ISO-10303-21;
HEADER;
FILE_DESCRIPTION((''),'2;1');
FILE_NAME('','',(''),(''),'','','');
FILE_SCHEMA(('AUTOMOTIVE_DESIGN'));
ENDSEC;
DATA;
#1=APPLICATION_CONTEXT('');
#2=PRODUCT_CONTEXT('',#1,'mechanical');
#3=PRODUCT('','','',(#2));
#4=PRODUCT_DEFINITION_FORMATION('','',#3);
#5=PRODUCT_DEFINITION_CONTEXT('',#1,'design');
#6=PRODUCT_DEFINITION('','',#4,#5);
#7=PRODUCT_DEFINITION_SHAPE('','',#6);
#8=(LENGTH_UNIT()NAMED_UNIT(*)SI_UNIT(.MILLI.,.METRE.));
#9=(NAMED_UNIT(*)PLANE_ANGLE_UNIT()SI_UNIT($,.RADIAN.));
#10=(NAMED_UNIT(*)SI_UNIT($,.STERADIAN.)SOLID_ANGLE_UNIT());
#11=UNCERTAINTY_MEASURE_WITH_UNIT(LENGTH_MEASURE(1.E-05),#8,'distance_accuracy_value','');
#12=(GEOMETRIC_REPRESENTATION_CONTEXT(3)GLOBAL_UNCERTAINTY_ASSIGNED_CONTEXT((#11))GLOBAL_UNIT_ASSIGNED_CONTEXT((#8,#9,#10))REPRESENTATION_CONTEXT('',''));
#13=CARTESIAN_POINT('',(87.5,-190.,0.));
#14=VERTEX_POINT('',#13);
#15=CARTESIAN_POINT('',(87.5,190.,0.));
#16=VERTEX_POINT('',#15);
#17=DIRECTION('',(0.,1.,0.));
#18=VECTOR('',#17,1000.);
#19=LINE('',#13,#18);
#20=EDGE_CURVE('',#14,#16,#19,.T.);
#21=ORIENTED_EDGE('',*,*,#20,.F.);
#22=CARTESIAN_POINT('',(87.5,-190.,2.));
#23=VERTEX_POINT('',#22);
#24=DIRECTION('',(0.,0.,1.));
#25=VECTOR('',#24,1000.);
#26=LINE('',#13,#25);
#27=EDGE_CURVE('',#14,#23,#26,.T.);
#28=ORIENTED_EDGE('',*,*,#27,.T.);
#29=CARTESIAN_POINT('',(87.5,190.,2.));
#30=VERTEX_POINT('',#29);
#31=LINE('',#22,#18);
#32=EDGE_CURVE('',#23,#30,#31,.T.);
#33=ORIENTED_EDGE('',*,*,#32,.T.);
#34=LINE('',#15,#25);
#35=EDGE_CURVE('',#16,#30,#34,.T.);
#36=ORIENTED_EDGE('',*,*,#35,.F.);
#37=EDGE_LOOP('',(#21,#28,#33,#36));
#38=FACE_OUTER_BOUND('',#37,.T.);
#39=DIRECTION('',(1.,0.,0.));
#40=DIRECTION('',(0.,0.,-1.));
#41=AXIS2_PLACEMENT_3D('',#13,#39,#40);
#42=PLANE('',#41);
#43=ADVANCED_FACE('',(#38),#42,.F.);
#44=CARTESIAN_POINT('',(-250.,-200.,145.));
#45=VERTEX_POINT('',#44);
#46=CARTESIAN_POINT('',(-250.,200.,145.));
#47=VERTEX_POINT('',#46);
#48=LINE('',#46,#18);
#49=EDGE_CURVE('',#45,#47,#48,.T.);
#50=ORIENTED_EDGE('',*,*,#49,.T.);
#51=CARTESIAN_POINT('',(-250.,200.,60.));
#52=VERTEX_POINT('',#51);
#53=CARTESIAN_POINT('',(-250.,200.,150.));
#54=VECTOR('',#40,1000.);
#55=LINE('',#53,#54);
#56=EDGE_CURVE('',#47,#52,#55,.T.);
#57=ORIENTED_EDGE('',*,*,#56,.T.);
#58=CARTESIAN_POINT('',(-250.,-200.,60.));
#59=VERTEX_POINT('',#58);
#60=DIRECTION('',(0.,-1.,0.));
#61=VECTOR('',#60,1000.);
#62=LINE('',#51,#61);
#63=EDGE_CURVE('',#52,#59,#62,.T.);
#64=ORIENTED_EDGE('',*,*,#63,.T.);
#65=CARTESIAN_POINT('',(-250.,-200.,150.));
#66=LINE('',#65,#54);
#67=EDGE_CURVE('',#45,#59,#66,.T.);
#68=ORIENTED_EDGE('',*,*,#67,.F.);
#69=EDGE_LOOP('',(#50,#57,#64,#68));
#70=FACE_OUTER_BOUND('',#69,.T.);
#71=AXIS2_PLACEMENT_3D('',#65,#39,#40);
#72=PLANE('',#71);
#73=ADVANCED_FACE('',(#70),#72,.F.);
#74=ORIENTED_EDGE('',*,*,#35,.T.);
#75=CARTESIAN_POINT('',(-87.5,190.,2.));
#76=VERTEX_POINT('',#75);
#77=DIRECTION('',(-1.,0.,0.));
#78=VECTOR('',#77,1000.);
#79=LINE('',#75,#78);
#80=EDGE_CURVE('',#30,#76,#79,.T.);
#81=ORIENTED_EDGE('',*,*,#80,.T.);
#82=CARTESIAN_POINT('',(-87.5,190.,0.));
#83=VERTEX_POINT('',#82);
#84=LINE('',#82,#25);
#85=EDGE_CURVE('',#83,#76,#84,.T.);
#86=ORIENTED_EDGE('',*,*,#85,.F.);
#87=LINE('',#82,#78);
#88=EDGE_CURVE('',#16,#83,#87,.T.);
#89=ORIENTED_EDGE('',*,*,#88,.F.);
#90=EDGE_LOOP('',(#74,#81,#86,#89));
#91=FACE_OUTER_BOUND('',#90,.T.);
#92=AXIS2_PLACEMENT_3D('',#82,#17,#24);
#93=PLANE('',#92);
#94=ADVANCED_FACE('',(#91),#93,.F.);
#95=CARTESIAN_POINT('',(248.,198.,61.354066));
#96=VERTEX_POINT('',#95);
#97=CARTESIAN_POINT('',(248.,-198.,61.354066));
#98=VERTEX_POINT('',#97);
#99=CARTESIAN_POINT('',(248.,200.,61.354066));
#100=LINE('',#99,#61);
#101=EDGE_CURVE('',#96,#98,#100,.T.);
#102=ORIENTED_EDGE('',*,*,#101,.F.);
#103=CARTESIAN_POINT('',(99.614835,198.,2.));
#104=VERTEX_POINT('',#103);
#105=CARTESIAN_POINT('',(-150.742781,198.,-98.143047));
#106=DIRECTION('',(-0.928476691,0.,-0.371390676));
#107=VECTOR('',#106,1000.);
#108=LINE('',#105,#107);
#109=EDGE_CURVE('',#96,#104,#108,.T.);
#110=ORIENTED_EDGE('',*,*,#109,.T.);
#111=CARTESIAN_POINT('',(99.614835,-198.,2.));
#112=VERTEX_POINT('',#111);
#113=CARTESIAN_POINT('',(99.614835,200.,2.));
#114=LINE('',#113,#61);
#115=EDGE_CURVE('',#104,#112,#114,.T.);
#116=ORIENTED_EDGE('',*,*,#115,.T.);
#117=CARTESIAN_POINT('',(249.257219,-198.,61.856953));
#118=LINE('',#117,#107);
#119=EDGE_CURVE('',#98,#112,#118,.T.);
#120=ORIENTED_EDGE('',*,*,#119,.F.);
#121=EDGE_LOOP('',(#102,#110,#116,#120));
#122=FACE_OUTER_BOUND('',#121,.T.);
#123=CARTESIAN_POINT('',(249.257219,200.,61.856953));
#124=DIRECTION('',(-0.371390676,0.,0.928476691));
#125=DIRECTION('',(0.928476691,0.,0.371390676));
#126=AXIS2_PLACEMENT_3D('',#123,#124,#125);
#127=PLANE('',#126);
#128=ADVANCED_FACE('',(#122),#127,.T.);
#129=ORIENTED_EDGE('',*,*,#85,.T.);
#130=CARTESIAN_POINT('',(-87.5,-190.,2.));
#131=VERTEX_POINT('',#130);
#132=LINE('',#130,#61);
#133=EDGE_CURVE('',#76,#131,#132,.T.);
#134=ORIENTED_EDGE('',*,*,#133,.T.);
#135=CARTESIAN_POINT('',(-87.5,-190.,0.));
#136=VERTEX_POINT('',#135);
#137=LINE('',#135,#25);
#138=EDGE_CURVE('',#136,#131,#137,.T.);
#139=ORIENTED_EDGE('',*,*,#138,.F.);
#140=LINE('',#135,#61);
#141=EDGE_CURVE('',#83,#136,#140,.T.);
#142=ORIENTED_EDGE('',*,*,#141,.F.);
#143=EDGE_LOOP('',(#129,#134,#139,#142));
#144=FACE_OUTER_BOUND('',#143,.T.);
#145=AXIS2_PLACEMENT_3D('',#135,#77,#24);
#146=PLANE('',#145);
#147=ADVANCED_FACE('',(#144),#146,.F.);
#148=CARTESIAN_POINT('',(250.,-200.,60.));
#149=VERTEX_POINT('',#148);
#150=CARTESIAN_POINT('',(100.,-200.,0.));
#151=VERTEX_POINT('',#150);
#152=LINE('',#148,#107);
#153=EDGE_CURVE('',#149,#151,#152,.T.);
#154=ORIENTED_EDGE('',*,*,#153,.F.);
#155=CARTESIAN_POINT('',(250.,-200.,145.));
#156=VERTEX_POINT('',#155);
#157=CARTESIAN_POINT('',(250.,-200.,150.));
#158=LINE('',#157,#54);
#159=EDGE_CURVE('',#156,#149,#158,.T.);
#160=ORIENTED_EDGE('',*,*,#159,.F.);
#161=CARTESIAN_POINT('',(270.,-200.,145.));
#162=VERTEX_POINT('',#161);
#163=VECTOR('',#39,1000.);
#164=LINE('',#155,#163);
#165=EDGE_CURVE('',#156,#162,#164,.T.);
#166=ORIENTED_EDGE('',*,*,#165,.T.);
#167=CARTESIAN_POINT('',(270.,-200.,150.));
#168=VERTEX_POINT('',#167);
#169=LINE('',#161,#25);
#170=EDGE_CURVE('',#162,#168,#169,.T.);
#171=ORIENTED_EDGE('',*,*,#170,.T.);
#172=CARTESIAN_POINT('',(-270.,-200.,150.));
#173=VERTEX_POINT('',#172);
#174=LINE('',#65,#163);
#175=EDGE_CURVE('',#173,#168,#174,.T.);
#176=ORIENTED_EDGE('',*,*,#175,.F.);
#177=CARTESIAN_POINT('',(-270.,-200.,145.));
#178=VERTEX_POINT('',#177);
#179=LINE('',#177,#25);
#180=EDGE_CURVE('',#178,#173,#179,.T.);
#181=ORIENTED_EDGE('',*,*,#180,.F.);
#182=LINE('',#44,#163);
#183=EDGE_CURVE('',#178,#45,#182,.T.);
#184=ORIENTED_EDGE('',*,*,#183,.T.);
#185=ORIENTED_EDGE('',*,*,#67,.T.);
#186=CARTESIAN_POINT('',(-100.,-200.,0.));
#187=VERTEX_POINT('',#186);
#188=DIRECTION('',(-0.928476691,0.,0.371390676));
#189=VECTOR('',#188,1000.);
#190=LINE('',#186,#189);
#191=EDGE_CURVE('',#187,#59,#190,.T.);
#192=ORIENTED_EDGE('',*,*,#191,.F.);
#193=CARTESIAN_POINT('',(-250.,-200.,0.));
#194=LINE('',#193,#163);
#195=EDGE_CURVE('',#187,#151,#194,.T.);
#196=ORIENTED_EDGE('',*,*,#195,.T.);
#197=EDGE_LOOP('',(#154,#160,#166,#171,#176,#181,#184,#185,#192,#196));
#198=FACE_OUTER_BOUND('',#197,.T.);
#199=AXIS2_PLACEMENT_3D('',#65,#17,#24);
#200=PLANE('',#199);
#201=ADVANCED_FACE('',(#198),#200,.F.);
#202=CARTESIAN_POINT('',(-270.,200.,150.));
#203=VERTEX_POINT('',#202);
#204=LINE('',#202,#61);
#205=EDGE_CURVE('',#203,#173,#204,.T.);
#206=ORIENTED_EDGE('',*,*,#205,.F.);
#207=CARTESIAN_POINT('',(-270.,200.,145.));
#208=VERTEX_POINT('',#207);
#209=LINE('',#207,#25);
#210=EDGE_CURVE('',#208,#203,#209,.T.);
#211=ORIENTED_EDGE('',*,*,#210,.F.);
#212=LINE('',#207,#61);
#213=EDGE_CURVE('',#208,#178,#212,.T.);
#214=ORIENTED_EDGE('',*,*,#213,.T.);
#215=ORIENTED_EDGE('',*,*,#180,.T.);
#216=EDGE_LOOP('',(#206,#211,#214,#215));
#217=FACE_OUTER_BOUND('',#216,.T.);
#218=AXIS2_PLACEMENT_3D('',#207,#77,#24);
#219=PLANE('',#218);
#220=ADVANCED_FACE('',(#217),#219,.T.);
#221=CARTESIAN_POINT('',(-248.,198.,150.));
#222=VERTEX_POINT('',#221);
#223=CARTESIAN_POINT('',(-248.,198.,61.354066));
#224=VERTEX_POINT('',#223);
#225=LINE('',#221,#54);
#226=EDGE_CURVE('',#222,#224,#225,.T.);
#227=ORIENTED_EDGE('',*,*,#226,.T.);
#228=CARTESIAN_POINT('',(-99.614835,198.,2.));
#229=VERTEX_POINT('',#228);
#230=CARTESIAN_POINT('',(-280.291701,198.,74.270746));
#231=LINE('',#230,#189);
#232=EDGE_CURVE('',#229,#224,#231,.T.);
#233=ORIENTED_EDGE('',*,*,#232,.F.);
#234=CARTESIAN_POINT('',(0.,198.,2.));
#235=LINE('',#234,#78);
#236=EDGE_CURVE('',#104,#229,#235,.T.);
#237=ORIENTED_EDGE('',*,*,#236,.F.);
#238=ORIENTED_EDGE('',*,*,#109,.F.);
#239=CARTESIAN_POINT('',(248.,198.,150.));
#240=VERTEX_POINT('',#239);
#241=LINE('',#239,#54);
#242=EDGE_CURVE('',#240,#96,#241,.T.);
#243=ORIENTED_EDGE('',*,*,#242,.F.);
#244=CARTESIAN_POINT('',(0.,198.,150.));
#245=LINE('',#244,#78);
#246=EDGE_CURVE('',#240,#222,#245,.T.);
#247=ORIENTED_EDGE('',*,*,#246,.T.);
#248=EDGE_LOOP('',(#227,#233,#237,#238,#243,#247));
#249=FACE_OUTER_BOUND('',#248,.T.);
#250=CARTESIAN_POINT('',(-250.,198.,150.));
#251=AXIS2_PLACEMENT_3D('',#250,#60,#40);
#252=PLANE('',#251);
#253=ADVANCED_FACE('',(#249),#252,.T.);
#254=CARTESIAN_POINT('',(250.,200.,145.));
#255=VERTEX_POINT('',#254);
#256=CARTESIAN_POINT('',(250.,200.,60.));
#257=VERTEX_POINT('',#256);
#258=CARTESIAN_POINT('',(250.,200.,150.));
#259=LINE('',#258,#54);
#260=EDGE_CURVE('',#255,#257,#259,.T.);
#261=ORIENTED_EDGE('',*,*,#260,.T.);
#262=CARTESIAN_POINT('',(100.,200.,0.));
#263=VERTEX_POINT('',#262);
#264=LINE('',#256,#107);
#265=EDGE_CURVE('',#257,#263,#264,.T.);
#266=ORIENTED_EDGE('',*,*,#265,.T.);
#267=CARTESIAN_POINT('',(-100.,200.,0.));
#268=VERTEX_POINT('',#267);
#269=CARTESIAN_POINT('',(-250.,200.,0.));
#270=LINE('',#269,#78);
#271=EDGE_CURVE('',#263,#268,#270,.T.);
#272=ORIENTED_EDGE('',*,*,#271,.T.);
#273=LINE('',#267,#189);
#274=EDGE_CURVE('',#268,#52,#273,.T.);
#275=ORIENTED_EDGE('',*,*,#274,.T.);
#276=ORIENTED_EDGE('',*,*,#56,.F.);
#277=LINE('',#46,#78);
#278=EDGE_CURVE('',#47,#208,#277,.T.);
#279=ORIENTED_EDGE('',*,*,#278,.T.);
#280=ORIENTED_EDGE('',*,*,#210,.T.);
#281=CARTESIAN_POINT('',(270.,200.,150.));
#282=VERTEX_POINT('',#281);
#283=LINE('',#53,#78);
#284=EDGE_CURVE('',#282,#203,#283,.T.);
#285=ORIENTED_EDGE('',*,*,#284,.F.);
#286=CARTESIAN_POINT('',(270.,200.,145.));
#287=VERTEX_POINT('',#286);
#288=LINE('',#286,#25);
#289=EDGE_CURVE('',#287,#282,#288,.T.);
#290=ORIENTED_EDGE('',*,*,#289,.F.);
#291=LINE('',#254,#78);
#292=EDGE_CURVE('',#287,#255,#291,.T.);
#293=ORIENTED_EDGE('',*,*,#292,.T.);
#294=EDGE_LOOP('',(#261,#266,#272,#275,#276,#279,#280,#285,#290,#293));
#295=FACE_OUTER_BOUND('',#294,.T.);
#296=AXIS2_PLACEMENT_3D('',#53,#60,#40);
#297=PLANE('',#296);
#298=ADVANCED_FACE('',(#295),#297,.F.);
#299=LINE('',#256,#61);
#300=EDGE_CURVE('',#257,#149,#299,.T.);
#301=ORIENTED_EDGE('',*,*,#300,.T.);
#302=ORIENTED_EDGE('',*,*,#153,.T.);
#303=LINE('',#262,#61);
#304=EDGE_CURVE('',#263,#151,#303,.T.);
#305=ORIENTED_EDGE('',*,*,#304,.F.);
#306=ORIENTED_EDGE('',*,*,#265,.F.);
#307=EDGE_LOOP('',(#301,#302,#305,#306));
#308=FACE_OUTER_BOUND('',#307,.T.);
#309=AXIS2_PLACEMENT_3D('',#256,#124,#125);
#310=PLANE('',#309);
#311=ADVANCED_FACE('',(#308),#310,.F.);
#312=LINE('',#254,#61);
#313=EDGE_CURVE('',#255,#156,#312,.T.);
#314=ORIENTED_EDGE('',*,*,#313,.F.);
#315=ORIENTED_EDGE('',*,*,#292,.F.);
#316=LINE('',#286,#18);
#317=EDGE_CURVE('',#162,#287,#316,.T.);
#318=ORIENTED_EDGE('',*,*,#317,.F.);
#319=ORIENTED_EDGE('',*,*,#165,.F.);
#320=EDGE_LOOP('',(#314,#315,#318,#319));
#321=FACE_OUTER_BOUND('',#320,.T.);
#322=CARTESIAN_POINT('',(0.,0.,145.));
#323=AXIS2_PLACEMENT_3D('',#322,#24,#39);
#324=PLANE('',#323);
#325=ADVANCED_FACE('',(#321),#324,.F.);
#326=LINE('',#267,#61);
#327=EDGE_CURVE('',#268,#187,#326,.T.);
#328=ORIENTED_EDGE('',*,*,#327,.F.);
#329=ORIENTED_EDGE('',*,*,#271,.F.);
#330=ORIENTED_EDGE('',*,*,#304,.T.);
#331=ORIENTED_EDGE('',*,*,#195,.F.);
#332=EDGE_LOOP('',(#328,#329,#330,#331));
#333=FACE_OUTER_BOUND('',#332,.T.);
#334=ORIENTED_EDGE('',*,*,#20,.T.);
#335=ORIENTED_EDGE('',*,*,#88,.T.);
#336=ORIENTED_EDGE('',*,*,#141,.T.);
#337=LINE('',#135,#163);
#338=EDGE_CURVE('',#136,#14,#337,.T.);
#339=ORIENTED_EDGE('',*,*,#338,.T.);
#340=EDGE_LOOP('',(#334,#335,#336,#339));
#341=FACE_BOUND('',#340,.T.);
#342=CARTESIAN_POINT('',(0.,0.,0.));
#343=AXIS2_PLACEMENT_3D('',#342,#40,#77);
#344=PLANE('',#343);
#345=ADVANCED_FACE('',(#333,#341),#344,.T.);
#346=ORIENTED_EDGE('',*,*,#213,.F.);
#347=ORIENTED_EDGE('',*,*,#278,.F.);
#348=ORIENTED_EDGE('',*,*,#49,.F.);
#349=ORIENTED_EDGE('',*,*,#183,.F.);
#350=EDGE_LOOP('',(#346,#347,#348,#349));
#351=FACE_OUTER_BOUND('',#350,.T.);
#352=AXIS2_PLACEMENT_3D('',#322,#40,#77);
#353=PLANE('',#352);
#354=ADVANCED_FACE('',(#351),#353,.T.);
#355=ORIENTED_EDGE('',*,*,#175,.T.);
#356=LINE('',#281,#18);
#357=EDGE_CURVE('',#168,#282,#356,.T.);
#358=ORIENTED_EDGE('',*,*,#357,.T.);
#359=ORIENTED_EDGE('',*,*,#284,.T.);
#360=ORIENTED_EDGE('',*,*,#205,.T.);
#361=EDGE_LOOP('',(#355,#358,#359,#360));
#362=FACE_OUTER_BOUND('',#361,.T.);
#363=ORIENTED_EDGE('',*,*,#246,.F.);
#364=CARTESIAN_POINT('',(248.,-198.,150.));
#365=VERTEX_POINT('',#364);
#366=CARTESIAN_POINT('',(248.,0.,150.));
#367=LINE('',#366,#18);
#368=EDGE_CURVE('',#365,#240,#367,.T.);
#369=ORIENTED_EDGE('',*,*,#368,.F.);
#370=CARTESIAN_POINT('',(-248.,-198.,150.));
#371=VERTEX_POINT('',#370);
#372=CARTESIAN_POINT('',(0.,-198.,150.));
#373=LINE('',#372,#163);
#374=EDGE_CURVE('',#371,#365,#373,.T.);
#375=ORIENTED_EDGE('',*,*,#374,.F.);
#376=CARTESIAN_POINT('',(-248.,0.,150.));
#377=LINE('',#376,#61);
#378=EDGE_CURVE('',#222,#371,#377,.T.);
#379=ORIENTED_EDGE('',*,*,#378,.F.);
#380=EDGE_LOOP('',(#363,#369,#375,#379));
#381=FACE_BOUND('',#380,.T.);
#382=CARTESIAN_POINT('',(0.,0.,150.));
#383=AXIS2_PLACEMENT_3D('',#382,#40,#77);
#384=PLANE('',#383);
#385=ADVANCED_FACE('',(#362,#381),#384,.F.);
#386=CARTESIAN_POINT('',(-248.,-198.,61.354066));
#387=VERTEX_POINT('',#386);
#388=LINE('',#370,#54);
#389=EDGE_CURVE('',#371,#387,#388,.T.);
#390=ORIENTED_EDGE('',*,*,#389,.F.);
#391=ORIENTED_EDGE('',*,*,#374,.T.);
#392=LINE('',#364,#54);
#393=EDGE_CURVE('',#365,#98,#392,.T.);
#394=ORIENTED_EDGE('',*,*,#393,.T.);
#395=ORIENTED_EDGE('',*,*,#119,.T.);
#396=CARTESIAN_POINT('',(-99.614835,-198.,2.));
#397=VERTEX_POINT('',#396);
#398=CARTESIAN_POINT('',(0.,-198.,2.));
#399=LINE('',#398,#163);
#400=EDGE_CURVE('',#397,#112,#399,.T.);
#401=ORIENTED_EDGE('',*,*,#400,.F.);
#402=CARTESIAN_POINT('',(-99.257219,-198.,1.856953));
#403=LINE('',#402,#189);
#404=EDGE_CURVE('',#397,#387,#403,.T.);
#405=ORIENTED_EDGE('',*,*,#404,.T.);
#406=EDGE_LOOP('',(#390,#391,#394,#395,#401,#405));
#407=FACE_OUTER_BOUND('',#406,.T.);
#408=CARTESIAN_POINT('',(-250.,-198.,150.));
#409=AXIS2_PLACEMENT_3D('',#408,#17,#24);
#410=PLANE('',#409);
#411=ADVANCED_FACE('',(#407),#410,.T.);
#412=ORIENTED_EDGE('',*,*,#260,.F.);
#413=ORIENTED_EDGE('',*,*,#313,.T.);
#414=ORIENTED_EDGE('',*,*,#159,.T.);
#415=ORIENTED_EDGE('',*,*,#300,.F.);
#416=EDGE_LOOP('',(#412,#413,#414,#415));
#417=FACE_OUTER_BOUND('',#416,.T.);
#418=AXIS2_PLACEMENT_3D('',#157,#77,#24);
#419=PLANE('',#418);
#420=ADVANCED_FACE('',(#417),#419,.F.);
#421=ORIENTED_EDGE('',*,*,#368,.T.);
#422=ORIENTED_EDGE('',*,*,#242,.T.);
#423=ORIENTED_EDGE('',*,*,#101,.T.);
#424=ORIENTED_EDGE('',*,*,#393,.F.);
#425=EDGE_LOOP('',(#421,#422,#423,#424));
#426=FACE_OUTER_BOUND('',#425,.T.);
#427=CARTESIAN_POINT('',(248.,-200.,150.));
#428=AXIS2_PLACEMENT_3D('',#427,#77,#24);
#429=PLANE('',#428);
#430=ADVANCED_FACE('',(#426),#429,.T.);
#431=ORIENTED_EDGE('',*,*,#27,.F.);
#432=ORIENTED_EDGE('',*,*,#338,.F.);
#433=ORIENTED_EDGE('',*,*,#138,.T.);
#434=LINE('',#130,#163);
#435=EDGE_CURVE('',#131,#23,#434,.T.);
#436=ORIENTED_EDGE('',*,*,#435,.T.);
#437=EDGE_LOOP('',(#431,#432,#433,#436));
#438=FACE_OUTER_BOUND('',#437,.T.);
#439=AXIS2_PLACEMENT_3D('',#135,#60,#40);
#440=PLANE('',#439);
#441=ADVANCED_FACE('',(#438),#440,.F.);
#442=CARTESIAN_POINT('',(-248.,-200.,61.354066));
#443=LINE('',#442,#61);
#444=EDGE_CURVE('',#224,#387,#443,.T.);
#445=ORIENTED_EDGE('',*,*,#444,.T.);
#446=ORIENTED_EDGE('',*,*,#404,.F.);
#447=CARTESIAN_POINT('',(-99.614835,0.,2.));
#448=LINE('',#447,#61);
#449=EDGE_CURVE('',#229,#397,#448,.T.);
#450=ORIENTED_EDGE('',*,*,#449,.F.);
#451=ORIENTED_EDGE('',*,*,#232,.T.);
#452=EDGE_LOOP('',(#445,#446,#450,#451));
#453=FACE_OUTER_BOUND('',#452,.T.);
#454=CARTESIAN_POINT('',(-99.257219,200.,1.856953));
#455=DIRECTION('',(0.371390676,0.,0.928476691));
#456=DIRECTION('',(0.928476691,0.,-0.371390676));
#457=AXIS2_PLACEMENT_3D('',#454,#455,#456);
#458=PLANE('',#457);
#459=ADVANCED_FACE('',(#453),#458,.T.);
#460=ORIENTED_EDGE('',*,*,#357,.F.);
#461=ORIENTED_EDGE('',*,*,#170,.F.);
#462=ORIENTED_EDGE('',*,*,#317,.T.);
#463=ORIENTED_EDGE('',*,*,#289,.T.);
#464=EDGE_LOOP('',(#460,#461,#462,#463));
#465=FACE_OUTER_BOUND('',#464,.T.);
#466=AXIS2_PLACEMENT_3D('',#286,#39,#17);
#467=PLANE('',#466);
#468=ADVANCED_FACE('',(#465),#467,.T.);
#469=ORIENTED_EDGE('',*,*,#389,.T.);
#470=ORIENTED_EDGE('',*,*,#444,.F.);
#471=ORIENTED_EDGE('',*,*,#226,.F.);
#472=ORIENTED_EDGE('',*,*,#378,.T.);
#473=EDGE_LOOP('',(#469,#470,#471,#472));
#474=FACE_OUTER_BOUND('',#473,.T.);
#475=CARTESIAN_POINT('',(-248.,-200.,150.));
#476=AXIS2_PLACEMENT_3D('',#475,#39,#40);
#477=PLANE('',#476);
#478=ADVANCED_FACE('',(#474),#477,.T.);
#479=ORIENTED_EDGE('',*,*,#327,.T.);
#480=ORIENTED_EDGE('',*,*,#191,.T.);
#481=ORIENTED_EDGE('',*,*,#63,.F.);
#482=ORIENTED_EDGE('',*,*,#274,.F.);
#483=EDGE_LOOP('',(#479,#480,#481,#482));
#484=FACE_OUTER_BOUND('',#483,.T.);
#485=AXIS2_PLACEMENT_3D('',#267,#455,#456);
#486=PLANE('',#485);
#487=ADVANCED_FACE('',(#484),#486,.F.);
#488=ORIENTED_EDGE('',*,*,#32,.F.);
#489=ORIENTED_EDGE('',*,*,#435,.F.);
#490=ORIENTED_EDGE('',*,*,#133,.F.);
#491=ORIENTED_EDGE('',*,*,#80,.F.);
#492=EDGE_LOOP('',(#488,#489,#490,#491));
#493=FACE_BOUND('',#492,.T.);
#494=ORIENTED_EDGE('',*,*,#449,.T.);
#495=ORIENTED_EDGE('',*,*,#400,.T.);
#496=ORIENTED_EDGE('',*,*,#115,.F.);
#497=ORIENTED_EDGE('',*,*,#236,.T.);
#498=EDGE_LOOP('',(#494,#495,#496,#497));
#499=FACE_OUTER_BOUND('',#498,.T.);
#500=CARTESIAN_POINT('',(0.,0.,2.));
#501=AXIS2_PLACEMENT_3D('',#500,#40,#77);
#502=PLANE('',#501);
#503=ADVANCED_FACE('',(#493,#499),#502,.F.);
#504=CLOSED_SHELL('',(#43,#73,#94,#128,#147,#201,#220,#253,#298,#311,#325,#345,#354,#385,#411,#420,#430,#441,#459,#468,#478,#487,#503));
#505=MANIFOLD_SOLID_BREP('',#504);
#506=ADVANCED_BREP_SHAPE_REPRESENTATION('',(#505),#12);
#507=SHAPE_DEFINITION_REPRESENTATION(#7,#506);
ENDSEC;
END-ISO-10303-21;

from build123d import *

# Parameters (mm, degrees)
SKETCH_1_W          = 500
SKETCH_1_H          = 400
EXTRUDE_1_DEPTH     = 150
CUT_EXTRUDE_1_DEPTH = 495.974746831
SHELL_1_T           = -2
SKETCH_2_W          = 20
SKETCH_2_H          = 400
EXTRUDE_2_DEPTH     = 5
SKETCH_4_W          = 175
SKETCH_4_H          = 380
CUT_EXTRUDE_2_DEPTH = 368.15664232


with BuildPart() as part:
    # 草图1 → 凸台-拉伸1 (new body)
    with BuildSketch(Plane.XY):
        Rectangle(SKETCH_1_W, SKETCH_1_H)
    extrude(amount=EXTRUDE_1_DEPTH)

    # 草图3 → 切除-拉伸1 (cut, through all)
    with BuildSketch(Plane.XZ.offset(200)):
        Polygon((-100, 0), (-250, 60), (-250, 0), align=None)
        Polygon((250, 60), (100, 0), (250, 0), align=None)
    extrude(amount=-CUT_EXTRUDE_1_DEPTH, mode=Mode.SUBTRACT)

    # 抽壳1
    shell_1_openings = [part.faces().sort_by_distance(p)[0] for p in [
        (0, 0, 150),
    ]]
    offset(amount=SHELL_1_T, openings=shell_1_openings, kind=Kind.INTERSECTION)

    # 草图2 → 凸台-拉伸2 (add)
    with BuildSketch(Plane.XY.offset(150)):
        with Locations((-260, 0)):
            Rectangle(SKETCH_2_W, SKETCH_2_H)
        with Locations((260, 0)):
            Rectangle(SKETCH_2_W, SKETCH_2_H)
    extrude(amount=-EXTRUDE_2_DEPTH)

    # 草图4 → 切除-拉伸2 (cut, through all)
    with BuildSketch(Plane.XY.offset(2)):
        Rectangle(SKETCH_4_W, SKETCH_4_H)
    extrude(amount=-CUT_EXTRUDE_2_DEPTH, mode=Mode.SUBTRACT)


solid = part.part
